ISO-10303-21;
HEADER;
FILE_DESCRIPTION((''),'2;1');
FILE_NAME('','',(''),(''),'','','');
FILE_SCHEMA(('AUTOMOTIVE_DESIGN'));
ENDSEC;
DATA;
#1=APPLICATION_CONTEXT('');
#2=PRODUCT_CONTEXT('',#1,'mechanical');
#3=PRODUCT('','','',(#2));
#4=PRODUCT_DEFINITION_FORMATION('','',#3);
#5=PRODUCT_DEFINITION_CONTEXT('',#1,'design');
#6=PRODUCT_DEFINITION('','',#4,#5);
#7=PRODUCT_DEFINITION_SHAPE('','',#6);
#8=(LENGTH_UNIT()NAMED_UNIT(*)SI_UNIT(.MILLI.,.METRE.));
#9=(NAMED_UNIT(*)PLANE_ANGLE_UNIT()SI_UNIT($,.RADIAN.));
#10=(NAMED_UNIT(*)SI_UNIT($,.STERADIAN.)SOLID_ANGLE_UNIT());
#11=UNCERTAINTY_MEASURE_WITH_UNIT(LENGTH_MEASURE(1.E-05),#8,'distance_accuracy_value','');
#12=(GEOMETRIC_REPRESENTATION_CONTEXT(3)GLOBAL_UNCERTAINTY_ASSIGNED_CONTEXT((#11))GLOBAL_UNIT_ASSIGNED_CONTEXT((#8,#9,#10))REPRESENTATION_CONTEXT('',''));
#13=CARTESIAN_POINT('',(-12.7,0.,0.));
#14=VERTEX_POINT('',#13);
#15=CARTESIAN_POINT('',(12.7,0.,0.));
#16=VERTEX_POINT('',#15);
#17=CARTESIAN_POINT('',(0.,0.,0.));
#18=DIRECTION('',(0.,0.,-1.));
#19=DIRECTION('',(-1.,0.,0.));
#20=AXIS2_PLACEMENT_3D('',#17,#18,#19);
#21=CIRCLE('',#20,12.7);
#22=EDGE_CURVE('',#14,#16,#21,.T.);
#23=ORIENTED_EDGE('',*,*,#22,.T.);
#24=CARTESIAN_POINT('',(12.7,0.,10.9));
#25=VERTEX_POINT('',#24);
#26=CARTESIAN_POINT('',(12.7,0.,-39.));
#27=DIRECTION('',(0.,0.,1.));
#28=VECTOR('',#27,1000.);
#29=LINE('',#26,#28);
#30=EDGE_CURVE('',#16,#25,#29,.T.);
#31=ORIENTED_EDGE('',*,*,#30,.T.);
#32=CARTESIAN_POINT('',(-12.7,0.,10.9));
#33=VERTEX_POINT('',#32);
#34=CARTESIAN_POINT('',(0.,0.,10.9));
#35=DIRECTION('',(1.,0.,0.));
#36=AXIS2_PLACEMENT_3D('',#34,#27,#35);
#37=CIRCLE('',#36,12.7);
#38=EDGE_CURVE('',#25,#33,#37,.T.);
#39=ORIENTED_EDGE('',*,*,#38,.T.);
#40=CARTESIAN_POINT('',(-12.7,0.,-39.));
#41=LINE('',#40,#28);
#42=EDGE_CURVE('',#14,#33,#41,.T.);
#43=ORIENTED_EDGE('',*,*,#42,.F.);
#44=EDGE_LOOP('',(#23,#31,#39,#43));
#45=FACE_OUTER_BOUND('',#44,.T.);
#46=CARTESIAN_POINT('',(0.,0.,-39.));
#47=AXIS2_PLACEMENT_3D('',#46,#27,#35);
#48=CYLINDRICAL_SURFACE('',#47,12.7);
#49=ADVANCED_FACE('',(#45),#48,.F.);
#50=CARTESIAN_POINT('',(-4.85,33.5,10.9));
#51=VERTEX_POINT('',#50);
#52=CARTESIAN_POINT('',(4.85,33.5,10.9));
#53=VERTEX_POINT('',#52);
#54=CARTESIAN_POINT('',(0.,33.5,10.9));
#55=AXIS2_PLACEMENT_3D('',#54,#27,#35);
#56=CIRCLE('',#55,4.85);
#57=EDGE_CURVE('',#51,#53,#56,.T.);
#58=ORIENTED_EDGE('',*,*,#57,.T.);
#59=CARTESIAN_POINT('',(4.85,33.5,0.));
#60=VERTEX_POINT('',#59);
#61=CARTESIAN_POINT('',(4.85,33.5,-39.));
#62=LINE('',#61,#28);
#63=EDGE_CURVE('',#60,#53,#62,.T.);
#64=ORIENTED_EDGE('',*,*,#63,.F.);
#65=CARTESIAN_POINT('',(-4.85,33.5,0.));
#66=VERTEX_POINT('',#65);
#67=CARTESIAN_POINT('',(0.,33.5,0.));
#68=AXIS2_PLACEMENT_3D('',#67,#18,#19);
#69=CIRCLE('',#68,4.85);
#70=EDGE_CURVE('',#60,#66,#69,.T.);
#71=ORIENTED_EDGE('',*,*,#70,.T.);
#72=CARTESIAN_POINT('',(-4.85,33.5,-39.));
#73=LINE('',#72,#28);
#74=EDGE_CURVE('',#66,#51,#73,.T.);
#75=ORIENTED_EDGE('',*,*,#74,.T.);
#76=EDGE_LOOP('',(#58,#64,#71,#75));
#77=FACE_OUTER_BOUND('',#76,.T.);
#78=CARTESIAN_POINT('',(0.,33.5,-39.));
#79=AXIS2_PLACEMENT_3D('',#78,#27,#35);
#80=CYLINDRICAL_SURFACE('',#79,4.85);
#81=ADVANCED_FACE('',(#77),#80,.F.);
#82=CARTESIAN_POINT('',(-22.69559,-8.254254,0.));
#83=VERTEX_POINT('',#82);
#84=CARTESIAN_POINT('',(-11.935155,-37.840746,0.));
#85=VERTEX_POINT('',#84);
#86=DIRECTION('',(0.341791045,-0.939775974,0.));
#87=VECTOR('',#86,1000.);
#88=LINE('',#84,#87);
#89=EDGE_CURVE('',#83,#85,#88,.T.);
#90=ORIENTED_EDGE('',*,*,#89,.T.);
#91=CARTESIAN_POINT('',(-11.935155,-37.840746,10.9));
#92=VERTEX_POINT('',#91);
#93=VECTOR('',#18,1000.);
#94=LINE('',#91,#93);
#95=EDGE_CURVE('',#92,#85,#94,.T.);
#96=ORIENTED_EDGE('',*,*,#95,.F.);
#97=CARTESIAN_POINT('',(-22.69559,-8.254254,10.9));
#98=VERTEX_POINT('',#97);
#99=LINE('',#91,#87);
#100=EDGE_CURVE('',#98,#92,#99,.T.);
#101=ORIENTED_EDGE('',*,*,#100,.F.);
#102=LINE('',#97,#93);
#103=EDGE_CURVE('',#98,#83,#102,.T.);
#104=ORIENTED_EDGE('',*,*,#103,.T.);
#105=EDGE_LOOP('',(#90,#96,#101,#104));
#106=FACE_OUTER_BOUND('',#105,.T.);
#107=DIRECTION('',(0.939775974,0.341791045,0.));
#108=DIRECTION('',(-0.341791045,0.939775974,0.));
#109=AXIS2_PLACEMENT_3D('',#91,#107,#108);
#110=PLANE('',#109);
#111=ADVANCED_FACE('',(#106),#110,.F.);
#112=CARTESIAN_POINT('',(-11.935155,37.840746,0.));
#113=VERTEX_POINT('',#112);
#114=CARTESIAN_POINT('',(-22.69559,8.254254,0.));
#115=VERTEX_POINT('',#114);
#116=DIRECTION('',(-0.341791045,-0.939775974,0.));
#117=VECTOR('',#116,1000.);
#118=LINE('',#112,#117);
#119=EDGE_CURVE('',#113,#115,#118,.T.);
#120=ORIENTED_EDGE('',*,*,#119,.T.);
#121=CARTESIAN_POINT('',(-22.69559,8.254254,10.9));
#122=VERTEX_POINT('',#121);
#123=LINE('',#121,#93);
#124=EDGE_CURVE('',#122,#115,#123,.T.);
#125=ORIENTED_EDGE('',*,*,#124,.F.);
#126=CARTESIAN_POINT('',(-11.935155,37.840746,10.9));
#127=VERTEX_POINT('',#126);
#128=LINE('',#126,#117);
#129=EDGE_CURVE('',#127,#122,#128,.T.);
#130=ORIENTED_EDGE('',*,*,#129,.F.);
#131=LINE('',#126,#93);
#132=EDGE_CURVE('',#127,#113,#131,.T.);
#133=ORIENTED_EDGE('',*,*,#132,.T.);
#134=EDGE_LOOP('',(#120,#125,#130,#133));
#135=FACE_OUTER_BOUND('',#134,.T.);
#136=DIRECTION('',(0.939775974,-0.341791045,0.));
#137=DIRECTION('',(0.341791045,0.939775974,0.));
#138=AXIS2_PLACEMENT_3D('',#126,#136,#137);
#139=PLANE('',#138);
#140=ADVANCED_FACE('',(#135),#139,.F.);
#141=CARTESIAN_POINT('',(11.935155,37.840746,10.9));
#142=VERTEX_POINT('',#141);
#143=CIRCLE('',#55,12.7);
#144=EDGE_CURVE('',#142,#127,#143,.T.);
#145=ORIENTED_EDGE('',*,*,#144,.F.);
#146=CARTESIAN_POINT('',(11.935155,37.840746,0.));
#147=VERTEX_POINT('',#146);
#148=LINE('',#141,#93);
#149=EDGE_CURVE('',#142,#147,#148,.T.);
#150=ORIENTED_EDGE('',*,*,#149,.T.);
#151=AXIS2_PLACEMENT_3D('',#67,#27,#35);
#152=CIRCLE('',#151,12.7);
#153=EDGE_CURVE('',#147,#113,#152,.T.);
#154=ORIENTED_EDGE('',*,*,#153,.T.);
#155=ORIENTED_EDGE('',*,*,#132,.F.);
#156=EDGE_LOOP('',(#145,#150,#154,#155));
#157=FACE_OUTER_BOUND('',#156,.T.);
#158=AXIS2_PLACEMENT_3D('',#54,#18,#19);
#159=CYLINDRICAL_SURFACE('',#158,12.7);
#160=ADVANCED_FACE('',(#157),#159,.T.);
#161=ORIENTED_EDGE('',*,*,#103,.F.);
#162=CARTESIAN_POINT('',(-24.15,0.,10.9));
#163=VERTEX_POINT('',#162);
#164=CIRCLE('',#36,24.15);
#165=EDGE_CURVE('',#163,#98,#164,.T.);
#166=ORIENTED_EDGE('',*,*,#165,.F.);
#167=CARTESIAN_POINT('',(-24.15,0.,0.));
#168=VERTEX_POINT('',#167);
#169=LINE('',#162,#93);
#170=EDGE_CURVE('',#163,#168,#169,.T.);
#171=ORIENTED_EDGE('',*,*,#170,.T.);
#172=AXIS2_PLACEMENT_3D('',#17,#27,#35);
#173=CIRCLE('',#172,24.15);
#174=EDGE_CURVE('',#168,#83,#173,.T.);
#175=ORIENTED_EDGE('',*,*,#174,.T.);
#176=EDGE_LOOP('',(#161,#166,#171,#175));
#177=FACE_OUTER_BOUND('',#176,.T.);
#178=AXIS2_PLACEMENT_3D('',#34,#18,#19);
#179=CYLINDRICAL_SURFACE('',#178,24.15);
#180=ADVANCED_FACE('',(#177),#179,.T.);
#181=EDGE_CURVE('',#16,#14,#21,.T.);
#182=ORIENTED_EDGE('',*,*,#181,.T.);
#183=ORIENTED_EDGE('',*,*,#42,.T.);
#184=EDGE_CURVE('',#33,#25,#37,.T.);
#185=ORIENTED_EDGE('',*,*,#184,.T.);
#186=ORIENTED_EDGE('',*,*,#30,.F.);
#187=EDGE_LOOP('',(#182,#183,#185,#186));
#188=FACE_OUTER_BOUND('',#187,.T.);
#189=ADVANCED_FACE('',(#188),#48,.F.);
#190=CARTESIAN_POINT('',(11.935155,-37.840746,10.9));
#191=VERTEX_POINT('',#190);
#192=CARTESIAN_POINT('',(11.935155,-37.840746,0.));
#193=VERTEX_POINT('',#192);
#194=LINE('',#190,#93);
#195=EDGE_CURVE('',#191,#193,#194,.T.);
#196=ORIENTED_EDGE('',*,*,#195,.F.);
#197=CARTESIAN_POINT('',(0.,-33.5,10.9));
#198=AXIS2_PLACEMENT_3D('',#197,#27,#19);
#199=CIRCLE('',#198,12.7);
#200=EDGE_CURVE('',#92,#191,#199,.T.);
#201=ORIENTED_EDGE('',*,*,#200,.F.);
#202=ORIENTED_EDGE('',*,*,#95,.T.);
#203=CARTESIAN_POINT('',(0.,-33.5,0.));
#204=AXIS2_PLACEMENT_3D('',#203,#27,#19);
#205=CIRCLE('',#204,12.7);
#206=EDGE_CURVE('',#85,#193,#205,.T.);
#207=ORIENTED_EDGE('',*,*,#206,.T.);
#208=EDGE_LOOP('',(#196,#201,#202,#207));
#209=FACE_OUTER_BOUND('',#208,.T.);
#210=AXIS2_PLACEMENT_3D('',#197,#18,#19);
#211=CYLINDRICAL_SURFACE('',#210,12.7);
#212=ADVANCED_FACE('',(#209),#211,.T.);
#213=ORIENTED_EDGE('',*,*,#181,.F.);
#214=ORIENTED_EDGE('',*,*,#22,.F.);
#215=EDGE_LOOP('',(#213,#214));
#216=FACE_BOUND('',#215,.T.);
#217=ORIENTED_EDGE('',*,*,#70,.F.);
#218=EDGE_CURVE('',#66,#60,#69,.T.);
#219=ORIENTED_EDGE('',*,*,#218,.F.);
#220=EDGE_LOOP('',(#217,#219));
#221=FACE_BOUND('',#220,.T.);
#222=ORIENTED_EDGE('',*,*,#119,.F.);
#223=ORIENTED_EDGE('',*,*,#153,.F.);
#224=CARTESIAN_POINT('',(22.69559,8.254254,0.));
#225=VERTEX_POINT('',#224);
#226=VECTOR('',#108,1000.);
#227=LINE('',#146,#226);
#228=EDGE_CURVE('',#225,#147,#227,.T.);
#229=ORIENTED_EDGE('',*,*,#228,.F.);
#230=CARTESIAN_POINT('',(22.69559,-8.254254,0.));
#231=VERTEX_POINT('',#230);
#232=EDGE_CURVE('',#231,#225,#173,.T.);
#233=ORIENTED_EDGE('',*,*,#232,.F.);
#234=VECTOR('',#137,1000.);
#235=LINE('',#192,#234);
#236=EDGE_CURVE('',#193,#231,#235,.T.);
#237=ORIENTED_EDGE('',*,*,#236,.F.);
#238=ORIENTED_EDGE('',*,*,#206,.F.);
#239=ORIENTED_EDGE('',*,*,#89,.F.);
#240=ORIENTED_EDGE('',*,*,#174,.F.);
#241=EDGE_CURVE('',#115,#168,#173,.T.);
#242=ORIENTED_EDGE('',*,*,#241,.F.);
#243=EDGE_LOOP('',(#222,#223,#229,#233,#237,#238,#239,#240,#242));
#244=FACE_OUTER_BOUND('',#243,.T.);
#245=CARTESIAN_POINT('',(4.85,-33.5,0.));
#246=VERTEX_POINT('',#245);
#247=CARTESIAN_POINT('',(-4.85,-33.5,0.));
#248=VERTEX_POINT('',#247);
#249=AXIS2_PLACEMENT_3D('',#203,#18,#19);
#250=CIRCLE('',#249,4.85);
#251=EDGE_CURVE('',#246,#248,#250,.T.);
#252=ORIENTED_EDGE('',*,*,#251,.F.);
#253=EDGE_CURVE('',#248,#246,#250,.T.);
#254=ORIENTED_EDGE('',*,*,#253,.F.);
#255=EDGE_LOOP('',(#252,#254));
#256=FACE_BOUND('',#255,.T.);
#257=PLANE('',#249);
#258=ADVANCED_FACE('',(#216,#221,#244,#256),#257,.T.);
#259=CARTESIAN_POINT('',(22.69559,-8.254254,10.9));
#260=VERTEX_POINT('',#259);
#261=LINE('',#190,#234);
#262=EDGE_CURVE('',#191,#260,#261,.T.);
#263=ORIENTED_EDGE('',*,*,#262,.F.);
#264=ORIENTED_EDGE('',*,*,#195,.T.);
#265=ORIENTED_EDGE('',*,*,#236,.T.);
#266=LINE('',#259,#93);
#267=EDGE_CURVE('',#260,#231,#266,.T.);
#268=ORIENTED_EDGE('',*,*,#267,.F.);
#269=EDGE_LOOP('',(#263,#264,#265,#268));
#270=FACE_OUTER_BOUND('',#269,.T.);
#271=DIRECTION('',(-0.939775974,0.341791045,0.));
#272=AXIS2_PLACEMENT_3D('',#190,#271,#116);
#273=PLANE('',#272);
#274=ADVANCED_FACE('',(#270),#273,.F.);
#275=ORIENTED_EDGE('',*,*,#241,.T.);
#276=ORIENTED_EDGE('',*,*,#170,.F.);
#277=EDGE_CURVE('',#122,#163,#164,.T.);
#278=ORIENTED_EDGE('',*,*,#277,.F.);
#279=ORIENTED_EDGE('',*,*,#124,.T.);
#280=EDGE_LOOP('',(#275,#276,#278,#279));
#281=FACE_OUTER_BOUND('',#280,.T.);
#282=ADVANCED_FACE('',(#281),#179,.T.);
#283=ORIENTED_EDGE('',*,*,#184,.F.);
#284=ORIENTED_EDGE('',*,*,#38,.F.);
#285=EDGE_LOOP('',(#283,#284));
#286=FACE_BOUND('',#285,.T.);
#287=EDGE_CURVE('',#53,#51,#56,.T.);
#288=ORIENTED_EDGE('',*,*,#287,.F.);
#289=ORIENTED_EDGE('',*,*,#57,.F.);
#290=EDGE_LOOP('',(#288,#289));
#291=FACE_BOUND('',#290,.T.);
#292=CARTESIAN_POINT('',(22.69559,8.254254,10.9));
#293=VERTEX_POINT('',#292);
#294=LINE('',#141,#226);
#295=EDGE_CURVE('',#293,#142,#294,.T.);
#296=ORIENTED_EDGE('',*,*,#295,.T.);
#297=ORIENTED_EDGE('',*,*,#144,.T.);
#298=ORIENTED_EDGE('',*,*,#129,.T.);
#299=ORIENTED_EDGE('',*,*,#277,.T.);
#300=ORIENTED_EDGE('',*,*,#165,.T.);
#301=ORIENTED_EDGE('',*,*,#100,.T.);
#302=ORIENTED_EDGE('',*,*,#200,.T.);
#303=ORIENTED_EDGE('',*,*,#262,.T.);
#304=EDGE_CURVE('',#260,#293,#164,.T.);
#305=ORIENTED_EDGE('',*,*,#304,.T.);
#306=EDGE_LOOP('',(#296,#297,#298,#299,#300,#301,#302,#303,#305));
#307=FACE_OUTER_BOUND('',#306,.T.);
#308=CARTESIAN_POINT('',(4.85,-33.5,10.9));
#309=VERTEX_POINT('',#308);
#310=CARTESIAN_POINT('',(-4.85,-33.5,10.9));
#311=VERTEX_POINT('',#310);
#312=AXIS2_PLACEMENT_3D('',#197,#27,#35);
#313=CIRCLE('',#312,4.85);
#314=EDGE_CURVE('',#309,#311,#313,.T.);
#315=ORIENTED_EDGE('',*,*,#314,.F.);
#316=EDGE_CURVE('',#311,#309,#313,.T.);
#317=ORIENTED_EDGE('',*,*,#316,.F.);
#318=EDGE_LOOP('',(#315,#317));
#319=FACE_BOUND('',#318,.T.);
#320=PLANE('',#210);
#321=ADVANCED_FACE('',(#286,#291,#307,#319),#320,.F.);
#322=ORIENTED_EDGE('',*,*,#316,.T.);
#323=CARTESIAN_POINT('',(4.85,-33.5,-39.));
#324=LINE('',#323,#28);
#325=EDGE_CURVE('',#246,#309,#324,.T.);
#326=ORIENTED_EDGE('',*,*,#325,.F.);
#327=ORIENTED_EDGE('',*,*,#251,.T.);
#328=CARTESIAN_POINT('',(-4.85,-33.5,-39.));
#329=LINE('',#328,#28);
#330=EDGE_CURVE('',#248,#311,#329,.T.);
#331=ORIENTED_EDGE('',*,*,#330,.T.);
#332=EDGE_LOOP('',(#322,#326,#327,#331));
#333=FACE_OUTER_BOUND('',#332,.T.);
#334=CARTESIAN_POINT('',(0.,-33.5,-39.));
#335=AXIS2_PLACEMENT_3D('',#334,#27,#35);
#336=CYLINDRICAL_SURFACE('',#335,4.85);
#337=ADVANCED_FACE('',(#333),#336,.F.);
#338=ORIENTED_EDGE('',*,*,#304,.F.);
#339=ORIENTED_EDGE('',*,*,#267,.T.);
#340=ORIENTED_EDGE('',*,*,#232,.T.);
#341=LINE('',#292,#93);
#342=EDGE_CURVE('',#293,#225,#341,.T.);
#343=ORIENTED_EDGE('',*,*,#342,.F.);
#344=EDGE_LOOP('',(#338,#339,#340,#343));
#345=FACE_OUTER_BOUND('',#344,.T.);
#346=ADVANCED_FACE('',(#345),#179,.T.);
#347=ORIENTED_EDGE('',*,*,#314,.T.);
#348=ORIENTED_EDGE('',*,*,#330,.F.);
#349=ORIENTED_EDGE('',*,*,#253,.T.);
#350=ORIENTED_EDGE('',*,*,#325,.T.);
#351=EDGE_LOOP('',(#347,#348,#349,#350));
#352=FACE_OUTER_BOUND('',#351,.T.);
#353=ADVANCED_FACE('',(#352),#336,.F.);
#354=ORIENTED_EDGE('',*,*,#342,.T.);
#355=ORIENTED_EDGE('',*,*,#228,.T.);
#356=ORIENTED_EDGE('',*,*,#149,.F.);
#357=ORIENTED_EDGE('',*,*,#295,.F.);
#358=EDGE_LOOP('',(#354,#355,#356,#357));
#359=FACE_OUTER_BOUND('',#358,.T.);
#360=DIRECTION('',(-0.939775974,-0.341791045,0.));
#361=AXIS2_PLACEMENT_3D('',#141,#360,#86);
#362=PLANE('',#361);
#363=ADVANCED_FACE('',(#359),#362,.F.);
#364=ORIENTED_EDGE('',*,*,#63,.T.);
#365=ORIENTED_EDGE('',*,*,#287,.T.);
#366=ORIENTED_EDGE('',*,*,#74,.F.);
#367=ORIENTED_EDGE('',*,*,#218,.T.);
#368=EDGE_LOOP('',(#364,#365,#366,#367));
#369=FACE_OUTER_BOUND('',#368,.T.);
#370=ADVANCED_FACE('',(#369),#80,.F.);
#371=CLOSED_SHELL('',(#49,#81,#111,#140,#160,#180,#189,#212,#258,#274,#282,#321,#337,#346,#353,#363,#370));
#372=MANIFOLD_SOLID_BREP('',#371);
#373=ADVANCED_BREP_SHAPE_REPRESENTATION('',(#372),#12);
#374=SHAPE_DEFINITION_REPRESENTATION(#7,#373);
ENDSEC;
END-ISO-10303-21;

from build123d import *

# Parameters (mm, degrees)
FLANGE_PLATE_10_9MM_DEPTH             = 10.9
BORE_AND_BOLT_HOLES_SKETCH_R          = 4.85
BORE_AND_BOLT_HOLES_SKETCH_R_2        = 12.7
BORE_25_4_AND_BOLT_HOLES_2X_9_7_DEPTH = 49.9


with BuildPart() as part:
    # Flange Outline Sketch → Flange Plate 10.9mm (new body)
    with BuildSketch(Plane.XY):
        with BuildLine():
            Line((-11.935154873, 37.840746269), (-22.695589777, 8.254253731))
            ThreePointArc((-22.695589777, 8.254253731), (-24.15, 0), (-22.695589777, -8.254253731))
            Line((-22.695589777, -8.254253731), (-11.935154873, -37.840746269))
            ThreePointArc((-11.935154873, -37.840746269), (0, -46.2), (11.935154873, -37.840746269))
            Line((11.935154873, -37.840746269), (22.695589777, -8.254253731))
            ThreePointArc((22.695589777, -8.254253731), (24.15, 0), (22.695589777, 8.254253731))
            Line((22.695589777, 8.254253731), (11.935154873, 37.840746269))
            ThreePointArc((11.935154873, 37.840746269), (0, 46.2), (-11.935154873, 37.840746269))
        make_face()
    extrude(amount=FLANGE_PLATE_10_9MM_DEPTH)

    # Bore and Bolt Holes Sketch → Bore Ø25.4 and Bolt Holes 2xØ9.7 (cut)
    with BuildSketch(Plane.XY.offset(10.9)):
        with Locations((0, 33.5)):
            Circle(BORE_AND_BOLT_HOLES_SKETCH_R)
        with Locations((0, -33.5)):
            Circle(BORE_AND_BOLT_HOLES_SKETCH_R)
        Circle(BORE_AND_BOLT_HOLES_SKETCH_R_2)
    extrude(amount=-BORE_25_4_AND_BOLT_HOLES_2X_9_7_DEPTH, mode=Mode.SUBTRACT)


solid = part.part
